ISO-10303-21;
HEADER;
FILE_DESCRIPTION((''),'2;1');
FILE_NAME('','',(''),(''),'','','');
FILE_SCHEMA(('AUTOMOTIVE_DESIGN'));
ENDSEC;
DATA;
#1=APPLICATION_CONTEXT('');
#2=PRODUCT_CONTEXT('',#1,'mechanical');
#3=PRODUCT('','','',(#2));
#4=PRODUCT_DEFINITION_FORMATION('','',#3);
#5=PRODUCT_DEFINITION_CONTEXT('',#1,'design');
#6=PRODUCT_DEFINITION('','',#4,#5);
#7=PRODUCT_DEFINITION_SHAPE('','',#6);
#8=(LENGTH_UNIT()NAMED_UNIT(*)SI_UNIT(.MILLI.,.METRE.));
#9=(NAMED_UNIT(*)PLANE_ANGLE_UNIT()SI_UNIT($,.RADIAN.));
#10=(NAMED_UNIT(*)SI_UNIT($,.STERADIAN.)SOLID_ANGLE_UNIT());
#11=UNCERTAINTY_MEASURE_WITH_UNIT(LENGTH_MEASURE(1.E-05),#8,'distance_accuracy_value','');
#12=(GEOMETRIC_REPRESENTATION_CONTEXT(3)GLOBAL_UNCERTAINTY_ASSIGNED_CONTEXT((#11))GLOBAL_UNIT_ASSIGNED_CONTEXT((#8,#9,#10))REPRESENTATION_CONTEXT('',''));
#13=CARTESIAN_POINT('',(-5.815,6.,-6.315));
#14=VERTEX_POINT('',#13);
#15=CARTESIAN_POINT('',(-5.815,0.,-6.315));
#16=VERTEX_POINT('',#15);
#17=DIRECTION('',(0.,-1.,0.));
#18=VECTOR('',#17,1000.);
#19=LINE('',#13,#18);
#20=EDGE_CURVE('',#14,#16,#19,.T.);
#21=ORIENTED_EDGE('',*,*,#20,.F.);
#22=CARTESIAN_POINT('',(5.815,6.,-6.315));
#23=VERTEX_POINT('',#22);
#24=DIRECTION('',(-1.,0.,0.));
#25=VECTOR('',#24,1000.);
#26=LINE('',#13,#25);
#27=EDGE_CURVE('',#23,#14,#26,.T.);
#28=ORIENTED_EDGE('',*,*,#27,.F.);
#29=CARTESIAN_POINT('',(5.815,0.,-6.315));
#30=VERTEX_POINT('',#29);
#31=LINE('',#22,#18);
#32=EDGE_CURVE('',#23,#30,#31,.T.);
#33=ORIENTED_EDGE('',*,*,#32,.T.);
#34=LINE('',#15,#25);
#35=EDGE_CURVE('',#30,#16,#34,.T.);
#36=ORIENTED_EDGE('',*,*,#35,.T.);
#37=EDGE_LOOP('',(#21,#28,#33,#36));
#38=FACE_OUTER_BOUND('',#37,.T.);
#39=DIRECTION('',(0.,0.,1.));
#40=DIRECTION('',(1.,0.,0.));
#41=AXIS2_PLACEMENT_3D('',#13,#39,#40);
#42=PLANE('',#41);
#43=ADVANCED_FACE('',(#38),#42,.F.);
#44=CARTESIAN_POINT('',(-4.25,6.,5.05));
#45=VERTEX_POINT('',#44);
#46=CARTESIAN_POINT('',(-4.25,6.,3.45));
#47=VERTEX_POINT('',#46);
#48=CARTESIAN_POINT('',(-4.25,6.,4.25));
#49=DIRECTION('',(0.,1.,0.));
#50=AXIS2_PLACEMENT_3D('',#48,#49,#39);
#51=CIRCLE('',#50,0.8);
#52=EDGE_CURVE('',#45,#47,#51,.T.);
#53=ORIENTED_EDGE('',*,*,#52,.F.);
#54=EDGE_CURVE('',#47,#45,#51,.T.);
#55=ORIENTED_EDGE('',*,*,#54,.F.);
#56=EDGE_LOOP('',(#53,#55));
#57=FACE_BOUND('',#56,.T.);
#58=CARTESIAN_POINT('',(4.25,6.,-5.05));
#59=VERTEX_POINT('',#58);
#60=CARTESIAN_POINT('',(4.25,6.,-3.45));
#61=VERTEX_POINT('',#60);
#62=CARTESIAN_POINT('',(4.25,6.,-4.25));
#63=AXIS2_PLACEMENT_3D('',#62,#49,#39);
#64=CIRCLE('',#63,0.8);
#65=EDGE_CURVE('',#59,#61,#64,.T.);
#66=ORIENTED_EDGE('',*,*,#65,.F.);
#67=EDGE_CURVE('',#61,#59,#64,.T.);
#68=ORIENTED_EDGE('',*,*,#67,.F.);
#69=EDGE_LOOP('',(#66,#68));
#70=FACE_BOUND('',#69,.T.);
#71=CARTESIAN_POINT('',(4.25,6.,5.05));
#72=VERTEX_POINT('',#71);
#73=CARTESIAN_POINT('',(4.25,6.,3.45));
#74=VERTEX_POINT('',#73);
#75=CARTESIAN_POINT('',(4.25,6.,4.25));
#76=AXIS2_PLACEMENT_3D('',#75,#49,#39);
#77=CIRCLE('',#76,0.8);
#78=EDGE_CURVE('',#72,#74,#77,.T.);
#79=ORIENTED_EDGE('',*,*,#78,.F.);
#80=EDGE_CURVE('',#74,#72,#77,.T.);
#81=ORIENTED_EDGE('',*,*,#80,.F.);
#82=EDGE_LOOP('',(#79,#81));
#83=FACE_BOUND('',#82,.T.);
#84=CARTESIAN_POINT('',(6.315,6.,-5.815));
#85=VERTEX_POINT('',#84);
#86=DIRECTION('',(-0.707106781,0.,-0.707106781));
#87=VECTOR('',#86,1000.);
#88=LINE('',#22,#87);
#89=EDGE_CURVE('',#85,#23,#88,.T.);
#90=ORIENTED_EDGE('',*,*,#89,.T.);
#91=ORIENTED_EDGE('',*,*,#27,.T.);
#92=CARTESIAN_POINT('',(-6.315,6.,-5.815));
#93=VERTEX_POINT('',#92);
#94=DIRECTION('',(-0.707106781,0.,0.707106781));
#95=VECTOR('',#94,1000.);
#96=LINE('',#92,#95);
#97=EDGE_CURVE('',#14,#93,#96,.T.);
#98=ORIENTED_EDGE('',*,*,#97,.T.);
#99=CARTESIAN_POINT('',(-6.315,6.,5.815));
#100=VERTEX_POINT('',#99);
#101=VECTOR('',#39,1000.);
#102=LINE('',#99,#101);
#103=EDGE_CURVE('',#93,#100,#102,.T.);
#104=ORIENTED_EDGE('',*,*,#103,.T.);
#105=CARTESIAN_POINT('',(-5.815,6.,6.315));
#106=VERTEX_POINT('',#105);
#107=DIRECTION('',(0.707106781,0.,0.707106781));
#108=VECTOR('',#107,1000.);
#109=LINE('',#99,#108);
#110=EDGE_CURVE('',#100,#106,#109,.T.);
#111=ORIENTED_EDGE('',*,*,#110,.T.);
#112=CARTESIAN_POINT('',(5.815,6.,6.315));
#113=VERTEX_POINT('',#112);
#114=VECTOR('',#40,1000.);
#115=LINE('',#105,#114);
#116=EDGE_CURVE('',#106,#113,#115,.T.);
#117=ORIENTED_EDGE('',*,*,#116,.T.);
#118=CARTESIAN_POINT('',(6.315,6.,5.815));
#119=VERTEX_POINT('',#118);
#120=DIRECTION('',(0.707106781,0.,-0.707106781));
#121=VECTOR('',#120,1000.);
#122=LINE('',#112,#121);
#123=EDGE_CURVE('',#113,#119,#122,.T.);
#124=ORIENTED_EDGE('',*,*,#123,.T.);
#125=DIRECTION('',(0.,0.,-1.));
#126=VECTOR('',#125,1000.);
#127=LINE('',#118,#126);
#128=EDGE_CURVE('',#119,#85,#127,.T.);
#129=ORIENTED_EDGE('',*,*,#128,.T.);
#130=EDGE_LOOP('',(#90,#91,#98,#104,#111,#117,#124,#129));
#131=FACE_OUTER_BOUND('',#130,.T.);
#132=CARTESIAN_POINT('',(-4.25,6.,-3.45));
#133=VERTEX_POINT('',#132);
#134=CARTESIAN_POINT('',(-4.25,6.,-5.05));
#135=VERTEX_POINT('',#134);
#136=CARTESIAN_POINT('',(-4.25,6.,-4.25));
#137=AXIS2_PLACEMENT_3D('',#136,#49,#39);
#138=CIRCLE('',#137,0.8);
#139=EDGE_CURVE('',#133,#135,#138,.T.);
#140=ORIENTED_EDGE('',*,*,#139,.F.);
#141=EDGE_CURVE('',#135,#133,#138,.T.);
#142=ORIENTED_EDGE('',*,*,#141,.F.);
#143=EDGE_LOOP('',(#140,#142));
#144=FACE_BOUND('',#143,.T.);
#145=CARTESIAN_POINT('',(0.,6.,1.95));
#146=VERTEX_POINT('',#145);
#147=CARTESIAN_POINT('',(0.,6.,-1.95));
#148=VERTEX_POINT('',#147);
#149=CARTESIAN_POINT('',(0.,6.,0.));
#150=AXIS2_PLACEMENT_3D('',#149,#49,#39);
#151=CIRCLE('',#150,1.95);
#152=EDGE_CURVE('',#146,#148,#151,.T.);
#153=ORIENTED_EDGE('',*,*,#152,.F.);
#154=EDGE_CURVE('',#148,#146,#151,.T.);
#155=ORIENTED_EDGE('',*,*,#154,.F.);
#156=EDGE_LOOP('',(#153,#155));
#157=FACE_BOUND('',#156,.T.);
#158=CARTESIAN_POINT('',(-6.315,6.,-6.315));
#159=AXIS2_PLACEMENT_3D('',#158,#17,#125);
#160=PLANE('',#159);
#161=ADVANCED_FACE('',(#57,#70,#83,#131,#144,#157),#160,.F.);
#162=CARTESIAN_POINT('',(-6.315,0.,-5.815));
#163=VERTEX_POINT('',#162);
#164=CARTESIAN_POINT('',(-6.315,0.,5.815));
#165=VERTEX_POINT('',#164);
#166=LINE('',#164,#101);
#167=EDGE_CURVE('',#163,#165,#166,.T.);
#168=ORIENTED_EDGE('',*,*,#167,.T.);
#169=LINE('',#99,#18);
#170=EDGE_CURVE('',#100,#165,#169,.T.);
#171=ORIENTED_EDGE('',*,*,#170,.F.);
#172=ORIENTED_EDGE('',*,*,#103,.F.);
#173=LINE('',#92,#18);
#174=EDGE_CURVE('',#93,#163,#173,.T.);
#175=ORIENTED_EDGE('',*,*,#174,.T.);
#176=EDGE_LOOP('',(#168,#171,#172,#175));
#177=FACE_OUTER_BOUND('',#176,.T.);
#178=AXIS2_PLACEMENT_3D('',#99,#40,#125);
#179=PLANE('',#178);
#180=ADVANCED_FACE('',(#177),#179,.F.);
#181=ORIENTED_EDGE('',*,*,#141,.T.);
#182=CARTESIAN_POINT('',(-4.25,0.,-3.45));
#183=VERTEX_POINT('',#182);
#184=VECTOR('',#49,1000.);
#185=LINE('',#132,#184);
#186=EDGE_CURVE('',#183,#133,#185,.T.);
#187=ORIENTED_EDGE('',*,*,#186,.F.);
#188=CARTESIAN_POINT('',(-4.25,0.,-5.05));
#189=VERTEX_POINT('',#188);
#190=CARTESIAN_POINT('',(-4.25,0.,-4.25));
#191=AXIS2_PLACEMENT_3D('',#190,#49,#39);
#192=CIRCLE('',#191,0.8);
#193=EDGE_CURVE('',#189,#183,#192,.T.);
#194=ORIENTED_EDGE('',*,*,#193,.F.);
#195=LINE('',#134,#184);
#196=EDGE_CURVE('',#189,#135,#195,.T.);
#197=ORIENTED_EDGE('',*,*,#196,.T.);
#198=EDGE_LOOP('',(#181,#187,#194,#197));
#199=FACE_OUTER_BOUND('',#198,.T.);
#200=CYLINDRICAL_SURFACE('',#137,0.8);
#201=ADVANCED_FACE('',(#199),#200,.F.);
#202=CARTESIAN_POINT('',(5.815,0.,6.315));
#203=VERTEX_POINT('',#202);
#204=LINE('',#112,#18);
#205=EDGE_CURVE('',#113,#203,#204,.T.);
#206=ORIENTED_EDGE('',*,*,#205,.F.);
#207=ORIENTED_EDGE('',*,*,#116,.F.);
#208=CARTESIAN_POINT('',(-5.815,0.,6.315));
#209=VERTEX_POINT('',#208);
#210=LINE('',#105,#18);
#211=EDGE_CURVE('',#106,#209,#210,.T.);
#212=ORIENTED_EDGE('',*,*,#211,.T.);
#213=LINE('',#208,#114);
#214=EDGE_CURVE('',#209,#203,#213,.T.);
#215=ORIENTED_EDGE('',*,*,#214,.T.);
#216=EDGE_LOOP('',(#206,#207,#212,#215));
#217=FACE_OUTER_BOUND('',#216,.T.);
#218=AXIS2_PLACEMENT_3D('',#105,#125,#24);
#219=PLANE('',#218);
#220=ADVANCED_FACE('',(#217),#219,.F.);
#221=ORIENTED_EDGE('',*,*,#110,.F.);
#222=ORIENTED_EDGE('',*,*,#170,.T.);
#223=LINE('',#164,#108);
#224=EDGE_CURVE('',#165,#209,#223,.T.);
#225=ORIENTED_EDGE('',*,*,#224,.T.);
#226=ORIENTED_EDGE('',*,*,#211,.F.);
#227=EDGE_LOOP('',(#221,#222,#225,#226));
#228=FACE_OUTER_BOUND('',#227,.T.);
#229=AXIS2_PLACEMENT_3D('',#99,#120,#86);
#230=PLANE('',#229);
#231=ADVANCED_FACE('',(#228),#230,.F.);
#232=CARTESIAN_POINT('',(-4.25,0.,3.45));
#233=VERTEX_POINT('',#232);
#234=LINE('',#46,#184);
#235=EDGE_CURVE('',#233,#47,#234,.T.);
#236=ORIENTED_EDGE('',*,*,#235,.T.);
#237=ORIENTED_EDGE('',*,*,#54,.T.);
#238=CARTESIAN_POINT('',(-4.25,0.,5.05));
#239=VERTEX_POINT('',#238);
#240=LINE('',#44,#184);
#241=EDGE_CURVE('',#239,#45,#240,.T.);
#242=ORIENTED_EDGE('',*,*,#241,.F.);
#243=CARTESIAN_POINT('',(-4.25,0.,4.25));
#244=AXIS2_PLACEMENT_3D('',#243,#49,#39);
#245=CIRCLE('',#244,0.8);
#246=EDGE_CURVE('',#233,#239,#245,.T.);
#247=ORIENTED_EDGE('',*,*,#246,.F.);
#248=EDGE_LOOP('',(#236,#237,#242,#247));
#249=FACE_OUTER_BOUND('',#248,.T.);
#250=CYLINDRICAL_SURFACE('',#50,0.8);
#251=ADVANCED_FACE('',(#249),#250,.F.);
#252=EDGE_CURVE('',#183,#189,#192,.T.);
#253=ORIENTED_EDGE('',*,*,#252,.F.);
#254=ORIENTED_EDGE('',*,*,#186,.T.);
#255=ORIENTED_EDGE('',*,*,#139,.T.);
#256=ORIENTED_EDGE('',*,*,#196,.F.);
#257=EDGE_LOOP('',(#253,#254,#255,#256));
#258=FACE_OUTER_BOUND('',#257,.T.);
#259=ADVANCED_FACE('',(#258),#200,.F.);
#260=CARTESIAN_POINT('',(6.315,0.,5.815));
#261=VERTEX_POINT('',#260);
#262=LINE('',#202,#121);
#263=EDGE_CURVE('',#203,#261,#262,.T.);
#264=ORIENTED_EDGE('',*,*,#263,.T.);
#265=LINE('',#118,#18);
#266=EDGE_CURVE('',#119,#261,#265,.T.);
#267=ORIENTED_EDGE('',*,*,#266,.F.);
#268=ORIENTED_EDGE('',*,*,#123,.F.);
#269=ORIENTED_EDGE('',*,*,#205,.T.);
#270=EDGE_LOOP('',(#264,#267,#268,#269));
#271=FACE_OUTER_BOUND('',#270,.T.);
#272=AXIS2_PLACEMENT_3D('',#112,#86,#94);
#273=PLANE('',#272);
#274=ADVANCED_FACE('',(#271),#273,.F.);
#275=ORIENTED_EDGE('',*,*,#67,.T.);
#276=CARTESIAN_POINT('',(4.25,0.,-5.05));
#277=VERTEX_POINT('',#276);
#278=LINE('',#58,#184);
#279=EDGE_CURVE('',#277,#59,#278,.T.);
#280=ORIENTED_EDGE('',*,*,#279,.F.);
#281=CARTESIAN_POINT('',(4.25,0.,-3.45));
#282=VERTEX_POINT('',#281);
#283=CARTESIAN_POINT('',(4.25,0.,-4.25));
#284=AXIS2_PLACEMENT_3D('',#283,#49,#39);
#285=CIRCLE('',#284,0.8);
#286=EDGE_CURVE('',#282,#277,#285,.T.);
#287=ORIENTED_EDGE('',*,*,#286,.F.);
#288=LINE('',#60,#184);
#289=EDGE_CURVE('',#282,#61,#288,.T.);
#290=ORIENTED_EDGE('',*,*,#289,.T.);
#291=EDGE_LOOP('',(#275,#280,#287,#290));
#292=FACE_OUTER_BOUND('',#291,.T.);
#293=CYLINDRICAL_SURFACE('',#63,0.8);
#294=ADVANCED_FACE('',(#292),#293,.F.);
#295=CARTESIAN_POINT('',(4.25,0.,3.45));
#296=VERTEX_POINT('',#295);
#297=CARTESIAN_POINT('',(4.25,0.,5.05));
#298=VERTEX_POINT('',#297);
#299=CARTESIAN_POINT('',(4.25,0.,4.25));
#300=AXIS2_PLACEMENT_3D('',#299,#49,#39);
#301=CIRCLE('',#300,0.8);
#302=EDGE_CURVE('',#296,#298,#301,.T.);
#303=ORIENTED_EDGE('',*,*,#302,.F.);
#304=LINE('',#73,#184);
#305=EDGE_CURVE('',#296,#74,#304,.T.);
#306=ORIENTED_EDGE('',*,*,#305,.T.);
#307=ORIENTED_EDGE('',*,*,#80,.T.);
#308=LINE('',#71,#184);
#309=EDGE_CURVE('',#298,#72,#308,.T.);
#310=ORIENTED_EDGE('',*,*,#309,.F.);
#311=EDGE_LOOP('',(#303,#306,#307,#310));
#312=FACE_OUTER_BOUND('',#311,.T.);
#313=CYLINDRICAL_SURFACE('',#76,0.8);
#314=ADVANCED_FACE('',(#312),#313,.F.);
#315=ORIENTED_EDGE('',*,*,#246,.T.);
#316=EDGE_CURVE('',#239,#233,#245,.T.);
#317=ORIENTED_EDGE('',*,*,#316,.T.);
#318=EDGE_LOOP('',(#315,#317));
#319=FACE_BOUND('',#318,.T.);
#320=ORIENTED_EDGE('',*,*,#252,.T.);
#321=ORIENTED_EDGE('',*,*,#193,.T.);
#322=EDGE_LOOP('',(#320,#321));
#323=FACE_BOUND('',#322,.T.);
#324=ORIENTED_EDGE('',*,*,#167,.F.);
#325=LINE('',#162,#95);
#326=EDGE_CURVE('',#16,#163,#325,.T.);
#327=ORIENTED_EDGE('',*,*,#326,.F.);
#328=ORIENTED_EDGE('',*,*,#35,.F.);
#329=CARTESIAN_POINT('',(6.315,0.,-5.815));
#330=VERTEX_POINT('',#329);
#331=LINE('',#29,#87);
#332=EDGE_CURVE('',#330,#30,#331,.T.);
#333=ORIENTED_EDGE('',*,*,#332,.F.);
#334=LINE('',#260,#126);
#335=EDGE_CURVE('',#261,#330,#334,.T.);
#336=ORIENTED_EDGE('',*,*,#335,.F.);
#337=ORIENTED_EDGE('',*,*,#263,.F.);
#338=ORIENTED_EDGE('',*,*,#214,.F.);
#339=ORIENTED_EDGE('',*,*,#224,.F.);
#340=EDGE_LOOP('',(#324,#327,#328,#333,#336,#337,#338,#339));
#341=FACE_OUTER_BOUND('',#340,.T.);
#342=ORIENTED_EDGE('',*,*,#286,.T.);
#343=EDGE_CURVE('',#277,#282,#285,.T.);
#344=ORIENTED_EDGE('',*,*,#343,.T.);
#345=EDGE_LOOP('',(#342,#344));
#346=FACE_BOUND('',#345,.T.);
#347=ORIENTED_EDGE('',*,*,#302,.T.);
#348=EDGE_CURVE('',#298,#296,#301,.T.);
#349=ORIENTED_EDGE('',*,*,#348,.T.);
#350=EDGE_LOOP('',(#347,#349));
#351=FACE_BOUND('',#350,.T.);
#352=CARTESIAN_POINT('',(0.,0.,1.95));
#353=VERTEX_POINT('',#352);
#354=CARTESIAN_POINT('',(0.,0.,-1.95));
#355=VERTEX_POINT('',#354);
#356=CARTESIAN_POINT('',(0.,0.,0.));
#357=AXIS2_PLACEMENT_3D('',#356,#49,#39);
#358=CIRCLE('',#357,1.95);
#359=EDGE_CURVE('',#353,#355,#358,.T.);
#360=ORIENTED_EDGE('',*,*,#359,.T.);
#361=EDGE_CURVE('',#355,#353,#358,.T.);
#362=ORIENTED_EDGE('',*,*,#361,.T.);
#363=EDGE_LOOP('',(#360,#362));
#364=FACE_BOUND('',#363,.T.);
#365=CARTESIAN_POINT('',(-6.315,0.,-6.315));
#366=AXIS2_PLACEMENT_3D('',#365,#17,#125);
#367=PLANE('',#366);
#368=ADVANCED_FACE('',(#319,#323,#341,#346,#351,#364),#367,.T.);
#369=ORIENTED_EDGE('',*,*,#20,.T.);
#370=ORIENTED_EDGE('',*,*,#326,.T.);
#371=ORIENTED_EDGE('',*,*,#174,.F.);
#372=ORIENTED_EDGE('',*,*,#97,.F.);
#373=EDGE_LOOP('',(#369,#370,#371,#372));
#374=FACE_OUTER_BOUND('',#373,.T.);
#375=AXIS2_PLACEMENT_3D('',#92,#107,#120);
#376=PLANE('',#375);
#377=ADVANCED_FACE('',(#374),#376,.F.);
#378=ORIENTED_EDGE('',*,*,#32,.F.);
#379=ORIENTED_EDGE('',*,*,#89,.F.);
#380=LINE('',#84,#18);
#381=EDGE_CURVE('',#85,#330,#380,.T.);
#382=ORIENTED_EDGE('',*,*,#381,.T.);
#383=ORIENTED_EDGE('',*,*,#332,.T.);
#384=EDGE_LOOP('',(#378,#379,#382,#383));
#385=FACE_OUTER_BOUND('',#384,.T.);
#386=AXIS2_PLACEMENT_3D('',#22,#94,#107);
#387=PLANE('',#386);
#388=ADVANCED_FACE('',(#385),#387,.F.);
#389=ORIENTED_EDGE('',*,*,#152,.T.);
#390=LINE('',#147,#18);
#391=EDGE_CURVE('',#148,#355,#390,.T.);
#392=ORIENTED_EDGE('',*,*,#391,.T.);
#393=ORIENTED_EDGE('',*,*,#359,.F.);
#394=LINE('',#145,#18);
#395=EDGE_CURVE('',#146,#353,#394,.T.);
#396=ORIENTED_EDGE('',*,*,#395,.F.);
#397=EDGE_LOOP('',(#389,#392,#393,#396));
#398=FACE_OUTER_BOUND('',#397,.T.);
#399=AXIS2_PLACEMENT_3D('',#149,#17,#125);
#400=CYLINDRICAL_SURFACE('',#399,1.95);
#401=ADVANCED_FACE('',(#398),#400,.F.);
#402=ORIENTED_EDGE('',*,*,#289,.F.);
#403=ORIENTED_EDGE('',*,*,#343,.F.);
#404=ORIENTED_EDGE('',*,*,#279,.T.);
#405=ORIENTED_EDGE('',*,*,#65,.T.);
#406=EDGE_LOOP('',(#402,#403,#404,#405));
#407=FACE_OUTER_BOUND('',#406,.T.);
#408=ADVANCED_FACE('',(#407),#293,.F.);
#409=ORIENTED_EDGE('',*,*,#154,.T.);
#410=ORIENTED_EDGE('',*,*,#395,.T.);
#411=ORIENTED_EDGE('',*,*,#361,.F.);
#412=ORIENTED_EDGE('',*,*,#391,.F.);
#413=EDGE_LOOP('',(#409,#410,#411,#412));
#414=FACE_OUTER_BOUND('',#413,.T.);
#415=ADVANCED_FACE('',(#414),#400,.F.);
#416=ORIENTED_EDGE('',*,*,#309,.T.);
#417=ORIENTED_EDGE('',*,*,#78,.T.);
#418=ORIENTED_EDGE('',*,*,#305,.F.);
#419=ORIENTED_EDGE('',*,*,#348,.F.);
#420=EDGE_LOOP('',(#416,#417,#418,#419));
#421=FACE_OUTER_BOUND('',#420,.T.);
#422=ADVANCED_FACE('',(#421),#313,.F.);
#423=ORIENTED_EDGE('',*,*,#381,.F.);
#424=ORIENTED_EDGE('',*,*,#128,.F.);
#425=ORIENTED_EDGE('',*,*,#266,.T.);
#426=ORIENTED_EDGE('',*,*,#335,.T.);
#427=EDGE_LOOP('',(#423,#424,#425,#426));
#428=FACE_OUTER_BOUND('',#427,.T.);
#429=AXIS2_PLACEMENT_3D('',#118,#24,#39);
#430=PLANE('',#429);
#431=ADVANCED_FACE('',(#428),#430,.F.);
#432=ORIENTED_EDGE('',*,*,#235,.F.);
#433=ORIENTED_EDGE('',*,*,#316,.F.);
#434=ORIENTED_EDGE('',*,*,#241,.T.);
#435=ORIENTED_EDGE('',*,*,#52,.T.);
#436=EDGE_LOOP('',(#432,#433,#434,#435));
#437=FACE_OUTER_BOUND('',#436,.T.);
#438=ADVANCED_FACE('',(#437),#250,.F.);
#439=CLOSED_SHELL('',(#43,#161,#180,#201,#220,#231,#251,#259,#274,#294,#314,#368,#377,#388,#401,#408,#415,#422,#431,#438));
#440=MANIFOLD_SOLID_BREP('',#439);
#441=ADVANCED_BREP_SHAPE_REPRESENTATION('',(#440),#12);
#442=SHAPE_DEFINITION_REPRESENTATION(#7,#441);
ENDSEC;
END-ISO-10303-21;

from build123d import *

# Parameters (mm, degrees)
SKETCH1_R             = 1.95
BOSS_EXTRUDE1_DEPTH   = 6
M2_TAPPED_HOLE2_D     = 1.6
M2_TAPPED_HOLE2_DEPTH = 6
M2_TAPPED_HOLE2_TIP   = 572.957422794


with BuildPart() as part:
    # Sketch1 → Boss-Extrude1 (new body)
    with BuildSketch(Plane(origin=(0, 0, 0), x_dir=(1, 0, 0), z_dir=(0, 1, 0))):
        Polygon((-6.315, 5.815), (-5.815, 6.315), (5.815, 6.315), (6.315, 5.815), (6.315, -5.815), (5.815, -6.315), (-5.815, -6.315), (-6.315, -5.815), align=None)
        with Locations(Location((0, 0, 0), (0, 0, 270))):
            Circle(SKETCH1_R, mode=Mode.SUBTRACT)
    extrude(amount=BOSS_EXTRUDE1_DEPTH)

    # M2 Tapped Hole2
    with Locations(Plane(origin=(0, 6, 0), x_dir=(-1, 0, 0), z_dir=(0, 1, 0))):
        with Locations((4.25, -4.25), (-4.25, -4.25), (-4.25, 4.25), (4.25, 4.25)):
            Hole(M2_TAPPED_HOLE2_D / 2, depth=M2_TAPPED_HOLE2_DEPTH)
            with Locations((0, 0, -(M2_TAPPED_HOLE2_DEPTH + M2_TAPPED_HOLE2_TIP / 2))):  # 0.16° drill point
                Cone(0, M2_TAPPED_HOLE2_D / 2, M2_TAPPED_HOLE2_TIP, mode=Mode.SUBTRACT)


solid = part.part
